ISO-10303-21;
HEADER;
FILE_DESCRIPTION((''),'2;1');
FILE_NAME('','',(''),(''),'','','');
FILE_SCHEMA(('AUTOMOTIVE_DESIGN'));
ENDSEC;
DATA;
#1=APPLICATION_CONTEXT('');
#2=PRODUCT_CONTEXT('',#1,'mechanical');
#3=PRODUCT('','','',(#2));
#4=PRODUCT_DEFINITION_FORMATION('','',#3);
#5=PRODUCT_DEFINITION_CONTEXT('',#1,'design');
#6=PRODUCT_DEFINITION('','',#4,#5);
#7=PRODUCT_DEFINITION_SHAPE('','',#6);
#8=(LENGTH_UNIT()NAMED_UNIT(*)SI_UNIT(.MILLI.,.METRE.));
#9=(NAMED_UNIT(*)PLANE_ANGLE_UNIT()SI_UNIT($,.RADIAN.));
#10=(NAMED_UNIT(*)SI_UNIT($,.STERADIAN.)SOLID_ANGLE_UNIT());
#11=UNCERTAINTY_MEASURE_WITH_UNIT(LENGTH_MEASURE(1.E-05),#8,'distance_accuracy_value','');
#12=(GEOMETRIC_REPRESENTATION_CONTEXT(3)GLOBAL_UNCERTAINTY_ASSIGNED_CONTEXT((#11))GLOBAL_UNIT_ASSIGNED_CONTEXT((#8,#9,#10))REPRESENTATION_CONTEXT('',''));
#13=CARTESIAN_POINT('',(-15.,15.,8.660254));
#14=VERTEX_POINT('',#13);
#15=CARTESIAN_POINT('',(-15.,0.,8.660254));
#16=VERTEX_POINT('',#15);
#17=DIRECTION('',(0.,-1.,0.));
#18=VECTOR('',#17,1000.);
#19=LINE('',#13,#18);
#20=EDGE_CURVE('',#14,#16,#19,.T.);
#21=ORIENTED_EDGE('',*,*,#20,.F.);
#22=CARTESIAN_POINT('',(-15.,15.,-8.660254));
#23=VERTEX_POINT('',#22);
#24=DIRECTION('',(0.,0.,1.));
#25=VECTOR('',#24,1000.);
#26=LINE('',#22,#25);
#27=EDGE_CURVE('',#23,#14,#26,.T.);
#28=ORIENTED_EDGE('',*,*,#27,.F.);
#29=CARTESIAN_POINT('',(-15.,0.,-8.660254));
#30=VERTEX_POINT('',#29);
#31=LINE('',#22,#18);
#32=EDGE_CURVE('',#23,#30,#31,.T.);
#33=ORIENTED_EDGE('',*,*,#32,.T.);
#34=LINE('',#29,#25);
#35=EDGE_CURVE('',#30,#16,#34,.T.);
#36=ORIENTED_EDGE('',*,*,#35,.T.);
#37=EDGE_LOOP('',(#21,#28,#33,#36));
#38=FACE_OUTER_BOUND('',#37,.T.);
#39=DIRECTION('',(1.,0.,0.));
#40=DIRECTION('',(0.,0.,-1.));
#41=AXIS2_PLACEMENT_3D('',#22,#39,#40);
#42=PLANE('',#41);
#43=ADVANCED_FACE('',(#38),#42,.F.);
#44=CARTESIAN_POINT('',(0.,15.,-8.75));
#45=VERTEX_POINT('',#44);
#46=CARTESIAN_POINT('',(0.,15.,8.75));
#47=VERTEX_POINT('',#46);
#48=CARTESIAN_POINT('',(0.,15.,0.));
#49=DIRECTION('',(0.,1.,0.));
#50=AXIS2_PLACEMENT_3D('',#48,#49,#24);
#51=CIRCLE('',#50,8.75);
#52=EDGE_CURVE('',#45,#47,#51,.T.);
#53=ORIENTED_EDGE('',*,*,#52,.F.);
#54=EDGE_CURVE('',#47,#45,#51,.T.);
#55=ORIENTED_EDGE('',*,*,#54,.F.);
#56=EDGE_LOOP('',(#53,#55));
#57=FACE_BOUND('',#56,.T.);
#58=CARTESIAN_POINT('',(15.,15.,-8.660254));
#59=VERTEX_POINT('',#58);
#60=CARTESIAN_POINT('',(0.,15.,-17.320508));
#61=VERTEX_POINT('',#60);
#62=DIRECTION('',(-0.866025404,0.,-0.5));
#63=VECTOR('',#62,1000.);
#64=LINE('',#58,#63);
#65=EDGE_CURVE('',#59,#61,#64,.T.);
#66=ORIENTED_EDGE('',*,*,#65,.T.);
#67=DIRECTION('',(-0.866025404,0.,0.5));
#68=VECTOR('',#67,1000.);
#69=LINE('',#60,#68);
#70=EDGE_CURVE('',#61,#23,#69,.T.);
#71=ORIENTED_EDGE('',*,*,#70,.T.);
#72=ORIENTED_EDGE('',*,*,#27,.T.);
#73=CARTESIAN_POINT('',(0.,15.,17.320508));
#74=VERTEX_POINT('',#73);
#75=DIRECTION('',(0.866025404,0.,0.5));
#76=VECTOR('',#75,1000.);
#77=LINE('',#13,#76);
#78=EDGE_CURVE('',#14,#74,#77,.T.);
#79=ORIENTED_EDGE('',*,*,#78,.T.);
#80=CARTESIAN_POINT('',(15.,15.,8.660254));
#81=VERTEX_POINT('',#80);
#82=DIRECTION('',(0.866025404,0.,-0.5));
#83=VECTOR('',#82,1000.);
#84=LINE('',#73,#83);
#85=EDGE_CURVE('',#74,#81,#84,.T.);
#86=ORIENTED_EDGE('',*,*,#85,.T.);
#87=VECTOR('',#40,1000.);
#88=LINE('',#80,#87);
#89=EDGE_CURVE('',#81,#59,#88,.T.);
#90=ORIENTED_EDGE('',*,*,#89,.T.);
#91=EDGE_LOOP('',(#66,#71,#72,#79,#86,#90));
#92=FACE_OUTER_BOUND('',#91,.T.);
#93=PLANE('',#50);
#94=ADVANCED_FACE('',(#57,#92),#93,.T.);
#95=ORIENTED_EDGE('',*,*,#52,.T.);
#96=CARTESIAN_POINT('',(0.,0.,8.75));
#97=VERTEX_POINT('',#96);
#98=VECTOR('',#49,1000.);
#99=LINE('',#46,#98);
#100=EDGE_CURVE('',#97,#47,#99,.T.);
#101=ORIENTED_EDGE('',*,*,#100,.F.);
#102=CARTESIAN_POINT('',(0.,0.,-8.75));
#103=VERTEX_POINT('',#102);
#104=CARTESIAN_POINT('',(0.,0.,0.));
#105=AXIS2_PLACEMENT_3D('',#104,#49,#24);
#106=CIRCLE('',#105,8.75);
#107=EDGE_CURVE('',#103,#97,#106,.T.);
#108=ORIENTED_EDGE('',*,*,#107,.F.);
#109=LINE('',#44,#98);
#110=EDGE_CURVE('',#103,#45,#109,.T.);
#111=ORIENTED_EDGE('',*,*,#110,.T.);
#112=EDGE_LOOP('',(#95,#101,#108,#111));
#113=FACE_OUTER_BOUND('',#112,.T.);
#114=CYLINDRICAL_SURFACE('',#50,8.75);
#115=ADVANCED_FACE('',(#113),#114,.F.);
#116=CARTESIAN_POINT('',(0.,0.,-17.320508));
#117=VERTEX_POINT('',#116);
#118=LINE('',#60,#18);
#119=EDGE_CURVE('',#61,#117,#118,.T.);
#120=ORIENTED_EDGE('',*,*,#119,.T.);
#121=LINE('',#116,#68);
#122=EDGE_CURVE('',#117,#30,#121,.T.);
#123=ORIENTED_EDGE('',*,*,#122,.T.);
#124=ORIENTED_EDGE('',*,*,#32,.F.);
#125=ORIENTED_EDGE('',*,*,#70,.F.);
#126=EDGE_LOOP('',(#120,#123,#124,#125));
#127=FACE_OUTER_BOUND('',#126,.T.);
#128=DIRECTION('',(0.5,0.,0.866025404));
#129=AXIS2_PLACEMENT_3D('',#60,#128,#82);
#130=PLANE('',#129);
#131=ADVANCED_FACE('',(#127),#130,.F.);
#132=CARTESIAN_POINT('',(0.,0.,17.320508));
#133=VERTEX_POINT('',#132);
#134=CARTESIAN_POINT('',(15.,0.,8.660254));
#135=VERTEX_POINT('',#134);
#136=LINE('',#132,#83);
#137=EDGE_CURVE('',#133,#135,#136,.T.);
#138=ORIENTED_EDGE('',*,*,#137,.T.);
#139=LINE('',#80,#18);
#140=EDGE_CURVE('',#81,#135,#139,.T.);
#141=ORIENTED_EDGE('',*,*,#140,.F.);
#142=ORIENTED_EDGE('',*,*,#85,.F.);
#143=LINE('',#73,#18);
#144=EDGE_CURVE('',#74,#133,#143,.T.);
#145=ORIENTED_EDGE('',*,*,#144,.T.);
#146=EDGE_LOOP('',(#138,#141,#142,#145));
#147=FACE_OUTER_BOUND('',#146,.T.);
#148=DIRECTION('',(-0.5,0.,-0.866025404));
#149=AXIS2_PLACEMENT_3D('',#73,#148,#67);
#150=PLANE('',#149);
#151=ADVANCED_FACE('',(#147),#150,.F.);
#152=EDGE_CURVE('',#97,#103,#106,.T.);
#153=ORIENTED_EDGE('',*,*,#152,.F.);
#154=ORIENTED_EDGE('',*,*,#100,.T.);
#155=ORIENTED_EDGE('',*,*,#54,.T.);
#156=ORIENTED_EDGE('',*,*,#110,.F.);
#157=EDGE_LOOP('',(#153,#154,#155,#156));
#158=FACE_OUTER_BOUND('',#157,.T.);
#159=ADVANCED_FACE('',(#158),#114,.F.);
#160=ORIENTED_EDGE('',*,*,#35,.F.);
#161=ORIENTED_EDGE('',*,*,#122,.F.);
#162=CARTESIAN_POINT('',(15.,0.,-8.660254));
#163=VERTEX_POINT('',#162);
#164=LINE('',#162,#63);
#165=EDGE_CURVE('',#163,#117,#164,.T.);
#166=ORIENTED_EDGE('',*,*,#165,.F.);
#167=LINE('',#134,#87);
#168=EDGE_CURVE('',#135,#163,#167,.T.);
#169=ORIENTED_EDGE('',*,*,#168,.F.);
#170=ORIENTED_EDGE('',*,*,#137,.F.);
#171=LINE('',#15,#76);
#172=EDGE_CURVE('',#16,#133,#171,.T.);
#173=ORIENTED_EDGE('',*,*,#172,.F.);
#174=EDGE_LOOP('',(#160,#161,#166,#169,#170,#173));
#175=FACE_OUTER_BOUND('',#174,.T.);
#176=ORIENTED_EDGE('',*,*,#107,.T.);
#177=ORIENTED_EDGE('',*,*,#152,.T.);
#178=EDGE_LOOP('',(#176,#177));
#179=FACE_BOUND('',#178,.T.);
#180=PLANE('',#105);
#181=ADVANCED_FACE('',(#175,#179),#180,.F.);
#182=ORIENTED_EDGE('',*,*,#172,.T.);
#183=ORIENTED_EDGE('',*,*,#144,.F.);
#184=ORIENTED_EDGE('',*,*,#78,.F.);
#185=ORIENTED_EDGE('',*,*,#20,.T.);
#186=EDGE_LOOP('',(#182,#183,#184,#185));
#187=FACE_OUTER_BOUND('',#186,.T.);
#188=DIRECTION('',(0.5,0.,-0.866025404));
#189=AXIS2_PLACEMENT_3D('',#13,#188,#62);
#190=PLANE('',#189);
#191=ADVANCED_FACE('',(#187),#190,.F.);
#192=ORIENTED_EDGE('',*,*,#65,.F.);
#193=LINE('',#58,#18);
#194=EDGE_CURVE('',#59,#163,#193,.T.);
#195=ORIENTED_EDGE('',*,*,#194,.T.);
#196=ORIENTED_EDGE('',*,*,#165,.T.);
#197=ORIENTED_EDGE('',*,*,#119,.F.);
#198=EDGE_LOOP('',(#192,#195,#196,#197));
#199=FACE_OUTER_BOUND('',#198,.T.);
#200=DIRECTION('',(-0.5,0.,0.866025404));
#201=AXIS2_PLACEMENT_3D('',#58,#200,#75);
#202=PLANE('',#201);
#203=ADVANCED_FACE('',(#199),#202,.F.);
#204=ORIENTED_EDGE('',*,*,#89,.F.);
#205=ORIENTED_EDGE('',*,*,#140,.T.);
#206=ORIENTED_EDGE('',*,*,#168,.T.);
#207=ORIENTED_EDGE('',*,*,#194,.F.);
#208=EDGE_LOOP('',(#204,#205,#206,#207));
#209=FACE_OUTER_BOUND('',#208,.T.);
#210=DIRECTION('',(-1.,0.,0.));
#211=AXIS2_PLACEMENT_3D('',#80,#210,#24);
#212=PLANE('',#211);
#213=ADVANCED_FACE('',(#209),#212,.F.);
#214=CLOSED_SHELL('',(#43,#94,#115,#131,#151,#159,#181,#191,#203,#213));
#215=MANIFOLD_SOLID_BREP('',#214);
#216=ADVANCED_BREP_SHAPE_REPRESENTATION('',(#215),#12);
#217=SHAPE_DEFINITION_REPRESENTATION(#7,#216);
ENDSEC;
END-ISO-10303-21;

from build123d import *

# Parameters (mm, degrees)
EXTRUDE_1_DEPTH     = 15
HOLE_WIZARD_M20_1_D = 17.5


with BuildPart() as part:
    # 草图1 → 凸台-拉伸1 (new body)
    with BuildSketch(Plane(origin=(0, 0, 0), x_dir=(1, 0, 0), z_dir=(0, 1, 0))):
        Polygon((0, 17.320508076), (-15, 8.660254038), (-15, -8.660254038), (0, -17.320508076), (15, -8.660254038), (15, 8.660254038), align=None)
    extrude(amount=EXTRUDE_1_DEPTH)

    # M20 螺纹孔1 (through all)
    with Locations(Plane(origin=(0, 15, 0), x_dir=(1, 0, 0), z_dir=(0, 1, 0))):
        with Locations((0, 0)):
            Hole(HOLE_WIZARD_M20_1_D / 2)


solid = part.part
